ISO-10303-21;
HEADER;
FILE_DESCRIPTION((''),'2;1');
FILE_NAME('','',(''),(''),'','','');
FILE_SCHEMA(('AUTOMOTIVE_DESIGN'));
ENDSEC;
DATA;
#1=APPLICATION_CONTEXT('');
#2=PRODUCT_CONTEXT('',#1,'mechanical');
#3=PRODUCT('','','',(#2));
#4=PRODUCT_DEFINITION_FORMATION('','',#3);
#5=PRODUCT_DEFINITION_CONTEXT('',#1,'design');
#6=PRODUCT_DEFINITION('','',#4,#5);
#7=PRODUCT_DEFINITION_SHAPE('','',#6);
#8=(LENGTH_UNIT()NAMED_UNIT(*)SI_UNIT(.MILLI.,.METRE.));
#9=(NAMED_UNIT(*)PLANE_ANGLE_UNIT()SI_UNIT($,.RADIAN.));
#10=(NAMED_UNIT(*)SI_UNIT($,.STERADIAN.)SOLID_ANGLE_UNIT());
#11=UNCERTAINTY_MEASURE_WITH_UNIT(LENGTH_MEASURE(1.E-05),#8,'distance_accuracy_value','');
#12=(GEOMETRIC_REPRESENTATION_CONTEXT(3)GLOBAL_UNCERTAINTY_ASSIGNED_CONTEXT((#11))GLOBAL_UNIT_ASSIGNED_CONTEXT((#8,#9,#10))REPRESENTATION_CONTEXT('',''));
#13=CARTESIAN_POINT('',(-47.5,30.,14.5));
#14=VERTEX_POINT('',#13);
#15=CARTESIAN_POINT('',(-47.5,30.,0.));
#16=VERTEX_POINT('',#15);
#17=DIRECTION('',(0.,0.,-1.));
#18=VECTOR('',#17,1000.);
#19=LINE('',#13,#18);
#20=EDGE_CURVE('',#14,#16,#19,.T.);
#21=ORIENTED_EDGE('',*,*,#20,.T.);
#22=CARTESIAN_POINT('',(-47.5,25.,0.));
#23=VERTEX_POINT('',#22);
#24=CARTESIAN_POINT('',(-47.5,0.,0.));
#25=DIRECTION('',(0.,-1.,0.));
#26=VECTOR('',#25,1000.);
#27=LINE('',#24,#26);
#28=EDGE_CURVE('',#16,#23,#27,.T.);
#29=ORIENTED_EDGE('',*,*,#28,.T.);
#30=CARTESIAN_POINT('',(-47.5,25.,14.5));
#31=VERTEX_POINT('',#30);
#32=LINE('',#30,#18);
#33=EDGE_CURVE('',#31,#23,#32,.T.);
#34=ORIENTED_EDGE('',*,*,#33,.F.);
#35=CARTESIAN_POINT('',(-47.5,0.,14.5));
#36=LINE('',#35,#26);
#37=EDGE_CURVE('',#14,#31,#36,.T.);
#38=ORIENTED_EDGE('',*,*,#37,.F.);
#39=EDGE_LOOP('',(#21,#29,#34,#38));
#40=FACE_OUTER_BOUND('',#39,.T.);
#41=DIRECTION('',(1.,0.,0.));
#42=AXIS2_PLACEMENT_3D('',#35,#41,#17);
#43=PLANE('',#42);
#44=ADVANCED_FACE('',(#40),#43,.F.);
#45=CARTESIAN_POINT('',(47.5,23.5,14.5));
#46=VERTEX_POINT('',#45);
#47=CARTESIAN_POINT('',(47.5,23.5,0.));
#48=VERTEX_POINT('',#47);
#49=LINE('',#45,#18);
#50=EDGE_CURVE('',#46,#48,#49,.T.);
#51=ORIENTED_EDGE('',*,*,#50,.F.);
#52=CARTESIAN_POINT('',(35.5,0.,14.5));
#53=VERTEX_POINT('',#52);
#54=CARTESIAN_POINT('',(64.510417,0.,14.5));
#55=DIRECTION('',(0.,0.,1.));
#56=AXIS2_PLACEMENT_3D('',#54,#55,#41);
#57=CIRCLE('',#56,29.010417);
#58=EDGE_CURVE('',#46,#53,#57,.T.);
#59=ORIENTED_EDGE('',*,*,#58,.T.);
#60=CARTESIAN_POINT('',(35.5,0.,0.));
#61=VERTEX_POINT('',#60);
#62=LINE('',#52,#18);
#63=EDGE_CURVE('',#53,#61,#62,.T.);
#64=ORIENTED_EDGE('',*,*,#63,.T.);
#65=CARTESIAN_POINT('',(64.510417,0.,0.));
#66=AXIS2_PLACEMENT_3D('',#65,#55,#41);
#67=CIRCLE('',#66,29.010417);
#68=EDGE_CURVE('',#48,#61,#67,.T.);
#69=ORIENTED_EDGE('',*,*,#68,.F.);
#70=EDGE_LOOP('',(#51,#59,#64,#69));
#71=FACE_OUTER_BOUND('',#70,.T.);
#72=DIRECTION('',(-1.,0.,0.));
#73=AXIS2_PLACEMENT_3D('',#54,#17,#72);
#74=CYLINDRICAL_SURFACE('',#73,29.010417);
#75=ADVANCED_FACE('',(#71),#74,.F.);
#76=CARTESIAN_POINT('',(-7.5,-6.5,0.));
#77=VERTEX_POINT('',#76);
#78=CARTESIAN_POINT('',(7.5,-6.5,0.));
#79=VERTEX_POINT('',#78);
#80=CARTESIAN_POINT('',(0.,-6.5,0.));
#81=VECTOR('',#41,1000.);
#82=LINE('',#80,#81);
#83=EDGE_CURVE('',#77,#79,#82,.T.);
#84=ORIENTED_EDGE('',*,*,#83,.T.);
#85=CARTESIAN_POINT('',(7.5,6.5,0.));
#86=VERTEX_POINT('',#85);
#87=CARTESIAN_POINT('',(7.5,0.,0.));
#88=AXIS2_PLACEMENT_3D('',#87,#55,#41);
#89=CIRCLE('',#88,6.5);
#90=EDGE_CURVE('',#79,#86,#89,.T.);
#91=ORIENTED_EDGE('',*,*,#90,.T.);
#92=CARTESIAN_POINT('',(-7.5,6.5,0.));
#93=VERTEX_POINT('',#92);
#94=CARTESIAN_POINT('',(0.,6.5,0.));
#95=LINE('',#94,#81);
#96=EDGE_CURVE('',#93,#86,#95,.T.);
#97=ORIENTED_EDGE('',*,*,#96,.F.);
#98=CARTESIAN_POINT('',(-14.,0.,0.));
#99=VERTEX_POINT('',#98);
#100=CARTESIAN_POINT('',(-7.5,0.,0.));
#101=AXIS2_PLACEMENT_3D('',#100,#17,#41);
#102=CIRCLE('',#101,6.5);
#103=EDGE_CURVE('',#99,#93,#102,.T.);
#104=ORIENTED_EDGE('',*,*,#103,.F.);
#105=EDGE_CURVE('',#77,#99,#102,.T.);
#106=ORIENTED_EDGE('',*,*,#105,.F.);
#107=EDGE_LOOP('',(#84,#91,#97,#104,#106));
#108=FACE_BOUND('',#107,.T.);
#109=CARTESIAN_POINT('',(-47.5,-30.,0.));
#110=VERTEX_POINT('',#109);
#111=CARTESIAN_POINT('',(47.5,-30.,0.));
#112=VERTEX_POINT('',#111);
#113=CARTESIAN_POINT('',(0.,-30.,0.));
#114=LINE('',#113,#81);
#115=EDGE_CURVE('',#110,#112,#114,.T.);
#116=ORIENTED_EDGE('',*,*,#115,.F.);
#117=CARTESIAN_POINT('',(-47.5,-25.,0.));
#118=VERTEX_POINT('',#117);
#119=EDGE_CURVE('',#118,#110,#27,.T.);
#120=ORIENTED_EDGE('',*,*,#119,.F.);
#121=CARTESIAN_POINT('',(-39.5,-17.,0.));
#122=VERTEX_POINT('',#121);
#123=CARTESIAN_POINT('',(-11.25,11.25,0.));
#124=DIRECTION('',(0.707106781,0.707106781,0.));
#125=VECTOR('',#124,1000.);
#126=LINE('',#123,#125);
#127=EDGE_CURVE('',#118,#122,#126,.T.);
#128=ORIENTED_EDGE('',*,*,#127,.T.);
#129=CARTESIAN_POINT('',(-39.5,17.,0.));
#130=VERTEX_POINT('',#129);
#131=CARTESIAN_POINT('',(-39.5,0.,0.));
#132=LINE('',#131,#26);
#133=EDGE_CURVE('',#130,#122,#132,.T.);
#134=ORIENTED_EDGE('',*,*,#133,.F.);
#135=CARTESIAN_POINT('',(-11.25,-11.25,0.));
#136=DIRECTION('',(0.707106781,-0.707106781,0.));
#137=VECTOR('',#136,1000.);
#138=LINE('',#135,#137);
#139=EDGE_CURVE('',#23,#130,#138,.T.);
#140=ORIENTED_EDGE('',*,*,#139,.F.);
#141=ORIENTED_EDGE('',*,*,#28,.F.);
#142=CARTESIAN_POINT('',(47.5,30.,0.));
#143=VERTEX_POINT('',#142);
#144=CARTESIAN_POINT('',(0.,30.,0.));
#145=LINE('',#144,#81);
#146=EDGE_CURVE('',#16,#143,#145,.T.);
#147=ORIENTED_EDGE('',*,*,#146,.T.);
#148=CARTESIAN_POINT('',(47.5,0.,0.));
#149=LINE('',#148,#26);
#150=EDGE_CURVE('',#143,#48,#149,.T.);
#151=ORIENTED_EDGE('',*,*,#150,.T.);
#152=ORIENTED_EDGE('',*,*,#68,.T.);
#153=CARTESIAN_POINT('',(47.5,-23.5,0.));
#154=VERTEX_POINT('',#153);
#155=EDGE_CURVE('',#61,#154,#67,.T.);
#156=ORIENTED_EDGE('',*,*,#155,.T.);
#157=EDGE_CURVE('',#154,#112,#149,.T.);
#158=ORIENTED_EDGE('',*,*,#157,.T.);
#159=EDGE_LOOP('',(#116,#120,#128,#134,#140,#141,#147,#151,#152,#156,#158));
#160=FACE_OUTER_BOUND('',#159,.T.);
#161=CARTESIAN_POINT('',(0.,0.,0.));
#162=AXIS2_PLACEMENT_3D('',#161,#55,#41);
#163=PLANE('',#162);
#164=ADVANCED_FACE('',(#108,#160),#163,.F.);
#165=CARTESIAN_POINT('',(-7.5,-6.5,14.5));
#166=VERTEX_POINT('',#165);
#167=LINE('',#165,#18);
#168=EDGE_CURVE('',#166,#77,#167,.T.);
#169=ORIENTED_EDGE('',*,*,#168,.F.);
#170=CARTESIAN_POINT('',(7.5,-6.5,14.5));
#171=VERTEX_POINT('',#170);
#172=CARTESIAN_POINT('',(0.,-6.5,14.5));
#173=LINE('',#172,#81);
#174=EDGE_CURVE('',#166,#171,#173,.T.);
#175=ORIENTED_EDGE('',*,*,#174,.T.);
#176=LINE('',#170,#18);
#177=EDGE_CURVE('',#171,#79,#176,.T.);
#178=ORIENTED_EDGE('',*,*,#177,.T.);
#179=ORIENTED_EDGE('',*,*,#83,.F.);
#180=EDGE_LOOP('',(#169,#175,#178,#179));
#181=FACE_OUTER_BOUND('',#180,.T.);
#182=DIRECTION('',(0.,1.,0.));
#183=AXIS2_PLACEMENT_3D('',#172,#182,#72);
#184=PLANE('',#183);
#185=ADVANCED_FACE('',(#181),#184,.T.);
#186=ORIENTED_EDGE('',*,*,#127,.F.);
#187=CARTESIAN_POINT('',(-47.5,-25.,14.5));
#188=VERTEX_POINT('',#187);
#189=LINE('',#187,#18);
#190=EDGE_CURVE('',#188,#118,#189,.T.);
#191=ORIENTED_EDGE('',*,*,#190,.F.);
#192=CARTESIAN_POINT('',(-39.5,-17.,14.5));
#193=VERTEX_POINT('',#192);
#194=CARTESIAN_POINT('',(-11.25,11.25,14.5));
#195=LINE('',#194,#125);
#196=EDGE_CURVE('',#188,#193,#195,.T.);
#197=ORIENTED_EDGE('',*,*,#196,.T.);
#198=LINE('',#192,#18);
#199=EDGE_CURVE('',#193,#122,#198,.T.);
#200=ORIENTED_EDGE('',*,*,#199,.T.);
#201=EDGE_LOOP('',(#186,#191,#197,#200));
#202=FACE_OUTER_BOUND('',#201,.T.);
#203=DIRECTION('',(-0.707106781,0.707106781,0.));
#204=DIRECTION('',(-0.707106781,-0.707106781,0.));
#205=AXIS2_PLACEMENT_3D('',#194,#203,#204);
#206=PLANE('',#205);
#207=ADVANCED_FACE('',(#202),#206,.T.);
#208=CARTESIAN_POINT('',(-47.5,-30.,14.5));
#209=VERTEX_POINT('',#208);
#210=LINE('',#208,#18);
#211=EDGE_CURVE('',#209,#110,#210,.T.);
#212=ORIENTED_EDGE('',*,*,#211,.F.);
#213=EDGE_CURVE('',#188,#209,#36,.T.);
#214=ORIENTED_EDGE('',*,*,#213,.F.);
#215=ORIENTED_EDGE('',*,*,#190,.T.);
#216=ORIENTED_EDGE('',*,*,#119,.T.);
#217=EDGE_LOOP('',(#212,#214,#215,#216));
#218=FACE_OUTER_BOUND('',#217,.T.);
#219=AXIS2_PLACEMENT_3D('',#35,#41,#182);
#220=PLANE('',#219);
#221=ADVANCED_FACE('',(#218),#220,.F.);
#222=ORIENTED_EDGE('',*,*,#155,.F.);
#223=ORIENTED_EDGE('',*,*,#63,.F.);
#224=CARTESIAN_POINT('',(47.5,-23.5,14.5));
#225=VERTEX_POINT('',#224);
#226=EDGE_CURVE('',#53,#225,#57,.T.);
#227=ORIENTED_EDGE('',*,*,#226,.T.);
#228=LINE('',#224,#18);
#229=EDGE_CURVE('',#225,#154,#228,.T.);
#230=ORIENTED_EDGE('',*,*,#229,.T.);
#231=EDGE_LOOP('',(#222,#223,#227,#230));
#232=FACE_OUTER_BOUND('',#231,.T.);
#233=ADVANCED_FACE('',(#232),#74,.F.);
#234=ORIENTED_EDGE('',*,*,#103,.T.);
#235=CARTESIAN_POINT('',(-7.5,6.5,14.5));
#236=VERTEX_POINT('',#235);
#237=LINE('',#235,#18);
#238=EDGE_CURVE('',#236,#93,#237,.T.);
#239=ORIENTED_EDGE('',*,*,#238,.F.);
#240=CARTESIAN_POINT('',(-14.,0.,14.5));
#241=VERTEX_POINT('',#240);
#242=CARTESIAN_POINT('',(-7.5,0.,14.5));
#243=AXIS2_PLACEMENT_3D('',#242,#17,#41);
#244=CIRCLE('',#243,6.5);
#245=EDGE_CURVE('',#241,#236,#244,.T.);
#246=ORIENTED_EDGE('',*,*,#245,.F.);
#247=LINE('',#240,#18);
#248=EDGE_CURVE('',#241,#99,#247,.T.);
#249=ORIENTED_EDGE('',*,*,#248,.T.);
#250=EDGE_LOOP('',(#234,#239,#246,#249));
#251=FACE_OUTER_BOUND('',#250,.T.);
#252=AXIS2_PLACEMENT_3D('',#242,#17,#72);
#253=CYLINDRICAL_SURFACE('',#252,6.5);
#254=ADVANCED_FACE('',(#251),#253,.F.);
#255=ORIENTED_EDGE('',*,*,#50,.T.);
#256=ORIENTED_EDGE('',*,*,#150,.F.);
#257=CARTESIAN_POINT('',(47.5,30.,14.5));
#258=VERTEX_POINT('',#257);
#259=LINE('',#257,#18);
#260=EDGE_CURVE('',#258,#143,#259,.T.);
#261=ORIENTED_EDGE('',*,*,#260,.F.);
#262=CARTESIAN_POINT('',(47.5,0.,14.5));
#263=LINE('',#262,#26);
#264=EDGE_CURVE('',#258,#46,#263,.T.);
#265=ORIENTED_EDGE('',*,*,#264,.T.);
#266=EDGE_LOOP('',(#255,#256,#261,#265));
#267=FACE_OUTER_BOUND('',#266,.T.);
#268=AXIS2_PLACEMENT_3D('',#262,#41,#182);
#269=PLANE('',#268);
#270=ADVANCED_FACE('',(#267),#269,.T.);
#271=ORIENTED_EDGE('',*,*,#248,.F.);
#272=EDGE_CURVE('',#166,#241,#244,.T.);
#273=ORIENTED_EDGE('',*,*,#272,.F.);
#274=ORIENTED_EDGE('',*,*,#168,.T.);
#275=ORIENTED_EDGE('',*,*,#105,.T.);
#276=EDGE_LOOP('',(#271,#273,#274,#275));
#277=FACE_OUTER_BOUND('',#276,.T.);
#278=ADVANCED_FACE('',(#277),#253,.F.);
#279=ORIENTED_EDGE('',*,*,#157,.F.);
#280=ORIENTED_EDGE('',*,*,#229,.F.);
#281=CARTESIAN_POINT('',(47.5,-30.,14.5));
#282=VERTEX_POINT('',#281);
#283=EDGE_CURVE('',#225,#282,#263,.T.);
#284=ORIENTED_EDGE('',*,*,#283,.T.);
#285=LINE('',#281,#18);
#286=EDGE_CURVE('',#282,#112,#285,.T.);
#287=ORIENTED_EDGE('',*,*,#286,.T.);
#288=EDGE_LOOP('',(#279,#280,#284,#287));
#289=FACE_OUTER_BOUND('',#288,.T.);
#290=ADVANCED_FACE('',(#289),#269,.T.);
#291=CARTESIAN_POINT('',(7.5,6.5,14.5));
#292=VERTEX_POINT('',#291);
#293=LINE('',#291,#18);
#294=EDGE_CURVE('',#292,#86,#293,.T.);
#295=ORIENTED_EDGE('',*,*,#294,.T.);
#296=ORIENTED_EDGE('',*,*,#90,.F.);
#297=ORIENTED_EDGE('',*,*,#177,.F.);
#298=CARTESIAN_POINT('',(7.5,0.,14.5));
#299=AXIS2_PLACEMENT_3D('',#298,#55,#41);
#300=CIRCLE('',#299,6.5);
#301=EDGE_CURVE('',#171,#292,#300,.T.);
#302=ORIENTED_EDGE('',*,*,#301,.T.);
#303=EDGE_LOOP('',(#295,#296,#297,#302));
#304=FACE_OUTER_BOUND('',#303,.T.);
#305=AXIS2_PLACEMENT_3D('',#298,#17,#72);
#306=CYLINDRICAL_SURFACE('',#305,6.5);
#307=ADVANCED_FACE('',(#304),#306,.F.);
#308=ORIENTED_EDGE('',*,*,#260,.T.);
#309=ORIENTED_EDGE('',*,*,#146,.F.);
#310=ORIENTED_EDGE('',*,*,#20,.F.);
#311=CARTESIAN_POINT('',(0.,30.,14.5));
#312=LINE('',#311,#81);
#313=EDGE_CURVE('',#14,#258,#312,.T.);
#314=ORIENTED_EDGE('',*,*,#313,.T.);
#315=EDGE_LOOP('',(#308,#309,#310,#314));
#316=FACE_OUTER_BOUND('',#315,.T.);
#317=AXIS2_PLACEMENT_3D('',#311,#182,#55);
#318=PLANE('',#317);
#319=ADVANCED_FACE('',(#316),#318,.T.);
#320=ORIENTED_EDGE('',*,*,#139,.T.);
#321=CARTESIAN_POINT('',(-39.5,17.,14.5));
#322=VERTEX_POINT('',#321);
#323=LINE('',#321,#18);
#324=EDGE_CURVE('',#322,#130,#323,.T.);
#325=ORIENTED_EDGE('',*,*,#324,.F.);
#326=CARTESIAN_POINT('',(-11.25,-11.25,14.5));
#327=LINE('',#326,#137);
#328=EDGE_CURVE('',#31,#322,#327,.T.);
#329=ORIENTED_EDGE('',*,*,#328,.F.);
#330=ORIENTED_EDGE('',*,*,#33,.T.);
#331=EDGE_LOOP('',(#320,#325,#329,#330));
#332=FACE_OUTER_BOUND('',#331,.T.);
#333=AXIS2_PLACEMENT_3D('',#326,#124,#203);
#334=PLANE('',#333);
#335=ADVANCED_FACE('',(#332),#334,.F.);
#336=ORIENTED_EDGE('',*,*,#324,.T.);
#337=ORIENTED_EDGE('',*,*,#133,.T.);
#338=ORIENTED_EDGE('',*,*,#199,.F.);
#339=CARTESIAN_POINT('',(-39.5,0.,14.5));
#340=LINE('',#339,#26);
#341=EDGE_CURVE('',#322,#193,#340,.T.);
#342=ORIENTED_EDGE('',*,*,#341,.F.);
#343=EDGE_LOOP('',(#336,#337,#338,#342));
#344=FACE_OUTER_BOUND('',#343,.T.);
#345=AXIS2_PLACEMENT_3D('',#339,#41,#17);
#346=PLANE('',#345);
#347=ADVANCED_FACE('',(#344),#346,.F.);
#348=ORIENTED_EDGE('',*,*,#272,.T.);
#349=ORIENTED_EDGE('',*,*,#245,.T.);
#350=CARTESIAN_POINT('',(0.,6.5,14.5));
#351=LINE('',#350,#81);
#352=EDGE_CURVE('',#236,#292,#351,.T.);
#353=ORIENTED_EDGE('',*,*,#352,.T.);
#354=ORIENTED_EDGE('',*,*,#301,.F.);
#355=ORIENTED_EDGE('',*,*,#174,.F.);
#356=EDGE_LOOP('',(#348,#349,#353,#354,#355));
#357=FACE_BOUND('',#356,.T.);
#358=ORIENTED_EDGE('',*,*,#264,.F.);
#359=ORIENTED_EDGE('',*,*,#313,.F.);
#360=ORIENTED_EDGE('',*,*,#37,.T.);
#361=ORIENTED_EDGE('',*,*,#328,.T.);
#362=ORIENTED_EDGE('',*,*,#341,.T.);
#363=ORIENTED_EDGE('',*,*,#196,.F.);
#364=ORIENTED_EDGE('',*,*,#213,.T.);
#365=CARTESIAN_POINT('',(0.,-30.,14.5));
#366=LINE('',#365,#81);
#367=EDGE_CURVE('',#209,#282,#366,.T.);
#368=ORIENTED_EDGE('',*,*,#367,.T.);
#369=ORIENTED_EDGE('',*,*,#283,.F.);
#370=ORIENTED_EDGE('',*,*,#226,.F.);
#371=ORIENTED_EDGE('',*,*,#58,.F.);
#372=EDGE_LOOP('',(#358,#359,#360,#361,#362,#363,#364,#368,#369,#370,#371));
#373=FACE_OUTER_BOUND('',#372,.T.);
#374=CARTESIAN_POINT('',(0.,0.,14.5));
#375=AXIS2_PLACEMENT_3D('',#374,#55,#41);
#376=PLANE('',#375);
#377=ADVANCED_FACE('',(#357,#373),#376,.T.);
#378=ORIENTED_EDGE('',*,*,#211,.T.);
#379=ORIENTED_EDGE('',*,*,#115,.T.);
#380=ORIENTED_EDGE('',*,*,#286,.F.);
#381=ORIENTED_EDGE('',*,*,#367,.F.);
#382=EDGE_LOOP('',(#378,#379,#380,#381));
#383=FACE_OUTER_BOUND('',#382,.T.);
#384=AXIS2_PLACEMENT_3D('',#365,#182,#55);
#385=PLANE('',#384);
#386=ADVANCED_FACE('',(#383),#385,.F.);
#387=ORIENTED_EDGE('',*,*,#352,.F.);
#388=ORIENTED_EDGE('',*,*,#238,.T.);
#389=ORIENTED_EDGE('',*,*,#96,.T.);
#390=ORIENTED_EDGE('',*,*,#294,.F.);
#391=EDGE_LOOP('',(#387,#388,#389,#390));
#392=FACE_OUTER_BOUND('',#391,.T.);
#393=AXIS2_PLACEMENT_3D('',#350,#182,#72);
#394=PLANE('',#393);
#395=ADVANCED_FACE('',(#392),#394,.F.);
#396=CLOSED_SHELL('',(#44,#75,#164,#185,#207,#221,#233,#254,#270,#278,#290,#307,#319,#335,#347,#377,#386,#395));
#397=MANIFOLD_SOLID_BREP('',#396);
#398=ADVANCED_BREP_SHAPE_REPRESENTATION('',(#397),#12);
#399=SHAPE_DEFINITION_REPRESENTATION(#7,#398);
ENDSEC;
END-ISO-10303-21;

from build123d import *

# Parameters (mm, degrees)
BOSS_EXTRUDE1_DEPTH = 14.5


with BuildPart() as part:
    # Sketch1 → Boss-Extrude1 (new body)
    with BuildSketch(Plane.XY):
        with BuildLine():
            ThreePointArc((47.5, 23.5), (35.5, 0), (47.5, -23.5))
            Line((47.5, -23.5), (47.5, -30))
            Line((47.5, -30), (-47.5, -30))
            Line((-47.5, -30), (-47.5, -25))
            Line((-47.5, -25), (-39.5, -17))
            Line((-39.5, -17), (-39.5, 17))
            Line((-39.5, 17), (-47.5, 25))
            Line((-47.5, 25), (-47.5, 30))
            Line((-47.5, 30), (47.5, 30))
            Line((47.5, 30), (47.5, 23.5))
        make_face()
        with BuildLine():
            Line((-7.5, -6.5), (7.5, -6.5))
            ThreePointArc((7.5, -6.5), (14, 0), (7.5, 6.5))
            Line((7.5, 6.5), (-7.5, 6.5))
            ThreePointArc((-7.5, 6.5), (-14, 0), (-7.5, -6.5))
        make_face(mode=Mode.SUBTRACT)
    extrude(amount=BOSS_EXTRUDE1_DEPTH)


solid = part.part
